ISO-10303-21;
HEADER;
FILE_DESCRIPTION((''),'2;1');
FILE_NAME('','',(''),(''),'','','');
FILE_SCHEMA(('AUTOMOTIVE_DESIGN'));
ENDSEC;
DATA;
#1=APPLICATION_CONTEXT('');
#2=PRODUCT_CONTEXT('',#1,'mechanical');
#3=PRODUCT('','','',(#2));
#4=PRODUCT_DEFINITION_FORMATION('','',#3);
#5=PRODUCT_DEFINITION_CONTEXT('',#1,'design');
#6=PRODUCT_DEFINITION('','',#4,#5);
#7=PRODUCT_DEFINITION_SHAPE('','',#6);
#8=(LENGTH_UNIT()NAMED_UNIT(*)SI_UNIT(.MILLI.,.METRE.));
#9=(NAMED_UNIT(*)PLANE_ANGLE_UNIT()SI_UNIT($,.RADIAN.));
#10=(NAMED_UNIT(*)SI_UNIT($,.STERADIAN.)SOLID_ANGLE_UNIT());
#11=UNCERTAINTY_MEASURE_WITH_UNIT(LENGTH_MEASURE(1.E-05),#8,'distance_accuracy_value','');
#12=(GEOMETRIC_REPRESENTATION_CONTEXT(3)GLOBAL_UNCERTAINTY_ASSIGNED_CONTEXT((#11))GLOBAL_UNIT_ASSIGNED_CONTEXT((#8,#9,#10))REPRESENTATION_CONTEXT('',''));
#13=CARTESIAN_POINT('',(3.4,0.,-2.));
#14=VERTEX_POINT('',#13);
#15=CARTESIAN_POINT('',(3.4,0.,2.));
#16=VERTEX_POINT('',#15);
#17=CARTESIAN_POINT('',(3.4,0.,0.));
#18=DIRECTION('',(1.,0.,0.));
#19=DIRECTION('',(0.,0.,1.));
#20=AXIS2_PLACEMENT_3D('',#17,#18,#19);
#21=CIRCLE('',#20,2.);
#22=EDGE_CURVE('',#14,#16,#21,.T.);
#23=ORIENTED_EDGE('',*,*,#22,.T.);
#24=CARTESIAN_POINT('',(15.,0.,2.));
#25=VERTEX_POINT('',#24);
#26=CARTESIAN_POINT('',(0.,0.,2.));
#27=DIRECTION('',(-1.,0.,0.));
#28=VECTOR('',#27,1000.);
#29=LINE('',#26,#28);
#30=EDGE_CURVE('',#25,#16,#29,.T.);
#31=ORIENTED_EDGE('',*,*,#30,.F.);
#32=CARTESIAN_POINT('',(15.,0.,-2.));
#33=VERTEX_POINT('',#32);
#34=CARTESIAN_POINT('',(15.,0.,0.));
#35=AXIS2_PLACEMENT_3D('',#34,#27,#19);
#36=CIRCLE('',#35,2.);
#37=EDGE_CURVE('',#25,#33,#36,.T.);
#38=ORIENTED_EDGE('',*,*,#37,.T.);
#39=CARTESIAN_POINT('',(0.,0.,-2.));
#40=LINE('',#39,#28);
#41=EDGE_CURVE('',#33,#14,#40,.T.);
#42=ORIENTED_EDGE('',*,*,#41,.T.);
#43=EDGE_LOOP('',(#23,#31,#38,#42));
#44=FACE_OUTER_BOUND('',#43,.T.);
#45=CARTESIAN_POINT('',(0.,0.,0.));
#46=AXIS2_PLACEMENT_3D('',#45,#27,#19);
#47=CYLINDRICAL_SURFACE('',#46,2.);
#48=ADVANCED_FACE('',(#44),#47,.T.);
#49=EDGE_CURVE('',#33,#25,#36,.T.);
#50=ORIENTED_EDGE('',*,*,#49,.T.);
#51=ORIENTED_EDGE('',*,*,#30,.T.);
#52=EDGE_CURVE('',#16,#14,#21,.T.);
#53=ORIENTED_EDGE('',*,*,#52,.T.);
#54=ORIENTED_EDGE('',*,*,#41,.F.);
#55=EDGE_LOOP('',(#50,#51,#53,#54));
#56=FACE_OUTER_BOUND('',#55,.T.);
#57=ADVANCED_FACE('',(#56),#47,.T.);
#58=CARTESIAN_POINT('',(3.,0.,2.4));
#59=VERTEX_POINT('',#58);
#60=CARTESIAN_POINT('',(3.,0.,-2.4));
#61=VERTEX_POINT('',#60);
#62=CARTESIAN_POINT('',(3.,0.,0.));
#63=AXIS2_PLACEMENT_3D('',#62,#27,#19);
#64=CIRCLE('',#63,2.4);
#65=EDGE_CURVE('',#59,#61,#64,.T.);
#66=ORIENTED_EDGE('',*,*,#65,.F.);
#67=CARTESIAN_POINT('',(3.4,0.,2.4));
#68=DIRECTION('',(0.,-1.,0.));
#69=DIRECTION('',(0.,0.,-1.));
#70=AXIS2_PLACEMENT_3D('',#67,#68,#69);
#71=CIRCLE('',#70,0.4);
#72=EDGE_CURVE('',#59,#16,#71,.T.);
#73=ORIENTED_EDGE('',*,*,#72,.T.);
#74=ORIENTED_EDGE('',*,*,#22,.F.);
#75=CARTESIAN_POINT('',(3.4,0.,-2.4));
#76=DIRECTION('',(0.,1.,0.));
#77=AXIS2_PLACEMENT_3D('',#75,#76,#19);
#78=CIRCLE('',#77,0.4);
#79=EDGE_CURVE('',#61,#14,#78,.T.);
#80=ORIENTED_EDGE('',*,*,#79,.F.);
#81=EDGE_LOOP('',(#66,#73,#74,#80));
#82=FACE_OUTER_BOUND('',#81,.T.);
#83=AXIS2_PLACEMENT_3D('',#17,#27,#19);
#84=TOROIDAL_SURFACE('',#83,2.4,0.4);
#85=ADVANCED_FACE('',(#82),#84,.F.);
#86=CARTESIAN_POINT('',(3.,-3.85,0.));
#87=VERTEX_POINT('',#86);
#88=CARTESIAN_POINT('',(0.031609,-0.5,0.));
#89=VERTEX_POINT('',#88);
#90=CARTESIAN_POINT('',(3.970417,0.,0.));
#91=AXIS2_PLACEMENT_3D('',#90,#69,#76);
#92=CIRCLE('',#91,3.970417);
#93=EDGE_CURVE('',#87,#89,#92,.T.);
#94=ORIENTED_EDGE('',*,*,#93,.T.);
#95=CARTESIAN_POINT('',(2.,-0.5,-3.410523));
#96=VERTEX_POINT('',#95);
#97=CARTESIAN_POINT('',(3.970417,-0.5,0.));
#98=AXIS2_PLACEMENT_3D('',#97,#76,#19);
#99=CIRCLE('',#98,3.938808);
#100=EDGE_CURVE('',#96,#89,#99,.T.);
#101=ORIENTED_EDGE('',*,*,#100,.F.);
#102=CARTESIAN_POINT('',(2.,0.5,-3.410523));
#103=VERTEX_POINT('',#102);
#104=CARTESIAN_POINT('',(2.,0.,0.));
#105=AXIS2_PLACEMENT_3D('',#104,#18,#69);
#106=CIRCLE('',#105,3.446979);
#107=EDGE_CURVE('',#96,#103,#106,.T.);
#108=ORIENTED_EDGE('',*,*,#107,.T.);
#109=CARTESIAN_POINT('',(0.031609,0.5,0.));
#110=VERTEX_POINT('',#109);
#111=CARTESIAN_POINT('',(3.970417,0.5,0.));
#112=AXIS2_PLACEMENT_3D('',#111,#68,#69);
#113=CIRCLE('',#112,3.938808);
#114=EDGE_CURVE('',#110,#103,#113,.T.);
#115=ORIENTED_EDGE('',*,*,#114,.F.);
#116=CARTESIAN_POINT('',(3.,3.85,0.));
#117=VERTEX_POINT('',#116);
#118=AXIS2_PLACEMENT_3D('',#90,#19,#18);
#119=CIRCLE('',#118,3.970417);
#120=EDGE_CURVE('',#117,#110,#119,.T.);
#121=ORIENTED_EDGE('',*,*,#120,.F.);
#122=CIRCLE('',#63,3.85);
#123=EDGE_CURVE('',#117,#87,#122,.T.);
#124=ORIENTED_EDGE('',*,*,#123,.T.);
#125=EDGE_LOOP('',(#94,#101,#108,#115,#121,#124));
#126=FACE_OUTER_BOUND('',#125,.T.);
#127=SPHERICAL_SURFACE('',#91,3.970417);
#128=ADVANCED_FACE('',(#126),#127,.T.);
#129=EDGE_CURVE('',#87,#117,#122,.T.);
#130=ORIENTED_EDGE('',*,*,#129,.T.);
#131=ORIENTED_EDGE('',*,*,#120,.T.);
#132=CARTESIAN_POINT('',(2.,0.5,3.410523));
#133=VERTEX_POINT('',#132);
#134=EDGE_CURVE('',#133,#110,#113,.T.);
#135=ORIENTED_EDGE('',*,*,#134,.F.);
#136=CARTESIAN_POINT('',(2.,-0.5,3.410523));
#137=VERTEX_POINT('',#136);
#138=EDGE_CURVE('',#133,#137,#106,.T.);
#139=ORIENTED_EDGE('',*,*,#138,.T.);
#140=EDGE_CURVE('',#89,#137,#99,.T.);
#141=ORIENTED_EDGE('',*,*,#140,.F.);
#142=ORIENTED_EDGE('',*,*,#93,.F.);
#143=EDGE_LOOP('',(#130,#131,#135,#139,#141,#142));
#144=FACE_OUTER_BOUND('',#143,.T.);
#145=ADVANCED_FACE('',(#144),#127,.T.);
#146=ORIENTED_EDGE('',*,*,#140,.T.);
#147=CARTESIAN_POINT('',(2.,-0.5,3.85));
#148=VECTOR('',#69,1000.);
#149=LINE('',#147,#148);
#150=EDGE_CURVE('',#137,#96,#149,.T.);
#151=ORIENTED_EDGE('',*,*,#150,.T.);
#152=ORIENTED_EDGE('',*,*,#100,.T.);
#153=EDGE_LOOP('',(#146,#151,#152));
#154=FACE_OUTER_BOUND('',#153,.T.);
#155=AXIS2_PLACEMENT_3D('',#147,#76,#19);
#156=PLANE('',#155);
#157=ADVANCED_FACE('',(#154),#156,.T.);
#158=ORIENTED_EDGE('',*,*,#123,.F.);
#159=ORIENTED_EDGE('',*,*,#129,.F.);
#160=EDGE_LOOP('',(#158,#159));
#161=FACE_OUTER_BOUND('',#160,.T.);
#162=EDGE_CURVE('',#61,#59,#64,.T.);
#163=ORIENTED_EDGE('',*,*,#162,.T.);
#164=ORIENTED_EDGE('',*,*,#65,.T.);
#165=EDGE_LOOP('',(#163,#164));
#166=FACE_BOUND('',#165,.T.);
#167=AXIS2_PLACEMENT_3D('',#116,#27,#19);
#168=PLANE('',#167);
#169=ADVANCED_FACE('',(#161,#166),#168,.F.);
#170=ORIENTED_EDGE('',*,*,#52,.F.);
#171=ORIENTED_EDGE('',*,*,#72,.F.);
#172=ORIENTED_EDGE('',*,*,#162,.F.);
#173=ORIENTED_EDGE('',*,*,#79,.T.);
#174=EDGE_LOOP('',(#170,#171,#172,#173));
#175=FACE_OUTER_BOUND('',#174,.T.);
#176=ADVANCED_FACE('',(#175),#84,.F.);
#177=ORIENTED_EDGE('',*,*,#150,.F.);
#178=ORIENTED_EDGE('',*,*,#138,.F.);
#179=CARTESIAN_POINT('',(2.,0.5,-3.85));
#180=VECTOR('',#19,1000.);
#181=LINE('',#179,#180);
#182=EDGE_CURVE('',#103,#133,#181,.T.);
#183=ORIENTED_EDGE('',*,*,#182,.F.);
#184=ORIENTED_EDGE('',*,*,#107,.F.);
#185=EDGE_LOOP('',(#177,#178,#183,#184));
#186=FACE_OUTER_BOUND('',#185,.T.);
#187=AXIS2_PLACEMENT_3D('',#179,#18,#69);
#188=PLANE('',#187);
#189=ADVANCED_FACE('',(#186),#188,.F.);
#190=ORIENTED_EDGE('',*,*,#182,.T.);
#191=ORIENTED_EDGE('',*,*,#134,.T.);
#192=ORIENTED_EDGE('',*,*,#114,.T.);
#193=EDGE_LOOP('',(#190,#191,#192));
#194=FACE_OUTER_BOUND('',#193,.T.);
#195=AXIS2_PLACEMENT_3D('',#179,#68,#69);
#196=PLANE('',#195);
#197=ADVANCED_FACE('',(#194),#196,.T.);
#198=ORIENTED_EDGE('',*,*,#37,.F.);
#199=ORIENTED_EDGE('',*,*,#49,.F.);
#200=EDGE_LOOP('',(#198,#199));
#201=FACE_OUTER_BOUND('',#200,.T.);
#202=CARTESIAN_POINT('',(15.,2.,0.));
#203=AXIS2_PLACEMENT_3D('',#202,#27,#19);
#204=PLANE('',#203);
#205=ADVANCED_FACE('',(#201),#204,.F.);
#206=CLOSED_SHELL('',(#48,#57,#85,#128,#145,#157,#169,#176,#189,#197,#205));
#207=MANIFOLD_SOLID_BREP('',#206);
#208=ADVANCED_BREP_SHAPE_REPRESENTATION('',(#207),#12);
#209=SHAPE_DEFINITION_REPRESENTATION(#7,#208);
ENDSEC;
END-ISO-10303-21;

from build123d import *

# Parameters (mm, degrees)
SKETCH_2_W          = 7.7
SKETCH_2_H          = 1
CUT_EXTRUDE_1_DEPTH = 2
FILLET_1_R          = 0.4


with BuildPart() as part:
    # 草图1 → 旋转1 (revolve)
    with BuildSketch(Plane.XY):
        with BuildLine():
            Line((3, 3.85), (3, 2))
            Line((3, 2), (7, 2))
            Line((7, 2), (15, 2))
            Line((15, 2), (15, 0))
            Line((15, 0), (0, 0))
            ThreePointArc((0, 0), (0.838550848, 2.440414924), (3, 3.85))
        make_face()
    revolve(axis=Axis((0, 0, 0), (1, 0, 0)))

    # 草图2 → 切除-拉伸1 (cut)
    with BuildSketch(Plane(origin=(0, 0, 0), x_dir=(0, 0, -1), z_dir=(1, 0, 0))):
        Rectangle(SKETCH_2_W, SKETCH_2_H)
    extrude(amount=CUT_EXTRUDE_1_DEPTH, mode=Mode.SUBTRACT)

    # 圆角1
    fillet_1_edges = [part.edges().sort_by_distance(p)[0] for p in [
        (3, -2, 0),
    ]]
    fillet(fillet_1_edges, radius=FILLET_1_R)


solid = part.part
